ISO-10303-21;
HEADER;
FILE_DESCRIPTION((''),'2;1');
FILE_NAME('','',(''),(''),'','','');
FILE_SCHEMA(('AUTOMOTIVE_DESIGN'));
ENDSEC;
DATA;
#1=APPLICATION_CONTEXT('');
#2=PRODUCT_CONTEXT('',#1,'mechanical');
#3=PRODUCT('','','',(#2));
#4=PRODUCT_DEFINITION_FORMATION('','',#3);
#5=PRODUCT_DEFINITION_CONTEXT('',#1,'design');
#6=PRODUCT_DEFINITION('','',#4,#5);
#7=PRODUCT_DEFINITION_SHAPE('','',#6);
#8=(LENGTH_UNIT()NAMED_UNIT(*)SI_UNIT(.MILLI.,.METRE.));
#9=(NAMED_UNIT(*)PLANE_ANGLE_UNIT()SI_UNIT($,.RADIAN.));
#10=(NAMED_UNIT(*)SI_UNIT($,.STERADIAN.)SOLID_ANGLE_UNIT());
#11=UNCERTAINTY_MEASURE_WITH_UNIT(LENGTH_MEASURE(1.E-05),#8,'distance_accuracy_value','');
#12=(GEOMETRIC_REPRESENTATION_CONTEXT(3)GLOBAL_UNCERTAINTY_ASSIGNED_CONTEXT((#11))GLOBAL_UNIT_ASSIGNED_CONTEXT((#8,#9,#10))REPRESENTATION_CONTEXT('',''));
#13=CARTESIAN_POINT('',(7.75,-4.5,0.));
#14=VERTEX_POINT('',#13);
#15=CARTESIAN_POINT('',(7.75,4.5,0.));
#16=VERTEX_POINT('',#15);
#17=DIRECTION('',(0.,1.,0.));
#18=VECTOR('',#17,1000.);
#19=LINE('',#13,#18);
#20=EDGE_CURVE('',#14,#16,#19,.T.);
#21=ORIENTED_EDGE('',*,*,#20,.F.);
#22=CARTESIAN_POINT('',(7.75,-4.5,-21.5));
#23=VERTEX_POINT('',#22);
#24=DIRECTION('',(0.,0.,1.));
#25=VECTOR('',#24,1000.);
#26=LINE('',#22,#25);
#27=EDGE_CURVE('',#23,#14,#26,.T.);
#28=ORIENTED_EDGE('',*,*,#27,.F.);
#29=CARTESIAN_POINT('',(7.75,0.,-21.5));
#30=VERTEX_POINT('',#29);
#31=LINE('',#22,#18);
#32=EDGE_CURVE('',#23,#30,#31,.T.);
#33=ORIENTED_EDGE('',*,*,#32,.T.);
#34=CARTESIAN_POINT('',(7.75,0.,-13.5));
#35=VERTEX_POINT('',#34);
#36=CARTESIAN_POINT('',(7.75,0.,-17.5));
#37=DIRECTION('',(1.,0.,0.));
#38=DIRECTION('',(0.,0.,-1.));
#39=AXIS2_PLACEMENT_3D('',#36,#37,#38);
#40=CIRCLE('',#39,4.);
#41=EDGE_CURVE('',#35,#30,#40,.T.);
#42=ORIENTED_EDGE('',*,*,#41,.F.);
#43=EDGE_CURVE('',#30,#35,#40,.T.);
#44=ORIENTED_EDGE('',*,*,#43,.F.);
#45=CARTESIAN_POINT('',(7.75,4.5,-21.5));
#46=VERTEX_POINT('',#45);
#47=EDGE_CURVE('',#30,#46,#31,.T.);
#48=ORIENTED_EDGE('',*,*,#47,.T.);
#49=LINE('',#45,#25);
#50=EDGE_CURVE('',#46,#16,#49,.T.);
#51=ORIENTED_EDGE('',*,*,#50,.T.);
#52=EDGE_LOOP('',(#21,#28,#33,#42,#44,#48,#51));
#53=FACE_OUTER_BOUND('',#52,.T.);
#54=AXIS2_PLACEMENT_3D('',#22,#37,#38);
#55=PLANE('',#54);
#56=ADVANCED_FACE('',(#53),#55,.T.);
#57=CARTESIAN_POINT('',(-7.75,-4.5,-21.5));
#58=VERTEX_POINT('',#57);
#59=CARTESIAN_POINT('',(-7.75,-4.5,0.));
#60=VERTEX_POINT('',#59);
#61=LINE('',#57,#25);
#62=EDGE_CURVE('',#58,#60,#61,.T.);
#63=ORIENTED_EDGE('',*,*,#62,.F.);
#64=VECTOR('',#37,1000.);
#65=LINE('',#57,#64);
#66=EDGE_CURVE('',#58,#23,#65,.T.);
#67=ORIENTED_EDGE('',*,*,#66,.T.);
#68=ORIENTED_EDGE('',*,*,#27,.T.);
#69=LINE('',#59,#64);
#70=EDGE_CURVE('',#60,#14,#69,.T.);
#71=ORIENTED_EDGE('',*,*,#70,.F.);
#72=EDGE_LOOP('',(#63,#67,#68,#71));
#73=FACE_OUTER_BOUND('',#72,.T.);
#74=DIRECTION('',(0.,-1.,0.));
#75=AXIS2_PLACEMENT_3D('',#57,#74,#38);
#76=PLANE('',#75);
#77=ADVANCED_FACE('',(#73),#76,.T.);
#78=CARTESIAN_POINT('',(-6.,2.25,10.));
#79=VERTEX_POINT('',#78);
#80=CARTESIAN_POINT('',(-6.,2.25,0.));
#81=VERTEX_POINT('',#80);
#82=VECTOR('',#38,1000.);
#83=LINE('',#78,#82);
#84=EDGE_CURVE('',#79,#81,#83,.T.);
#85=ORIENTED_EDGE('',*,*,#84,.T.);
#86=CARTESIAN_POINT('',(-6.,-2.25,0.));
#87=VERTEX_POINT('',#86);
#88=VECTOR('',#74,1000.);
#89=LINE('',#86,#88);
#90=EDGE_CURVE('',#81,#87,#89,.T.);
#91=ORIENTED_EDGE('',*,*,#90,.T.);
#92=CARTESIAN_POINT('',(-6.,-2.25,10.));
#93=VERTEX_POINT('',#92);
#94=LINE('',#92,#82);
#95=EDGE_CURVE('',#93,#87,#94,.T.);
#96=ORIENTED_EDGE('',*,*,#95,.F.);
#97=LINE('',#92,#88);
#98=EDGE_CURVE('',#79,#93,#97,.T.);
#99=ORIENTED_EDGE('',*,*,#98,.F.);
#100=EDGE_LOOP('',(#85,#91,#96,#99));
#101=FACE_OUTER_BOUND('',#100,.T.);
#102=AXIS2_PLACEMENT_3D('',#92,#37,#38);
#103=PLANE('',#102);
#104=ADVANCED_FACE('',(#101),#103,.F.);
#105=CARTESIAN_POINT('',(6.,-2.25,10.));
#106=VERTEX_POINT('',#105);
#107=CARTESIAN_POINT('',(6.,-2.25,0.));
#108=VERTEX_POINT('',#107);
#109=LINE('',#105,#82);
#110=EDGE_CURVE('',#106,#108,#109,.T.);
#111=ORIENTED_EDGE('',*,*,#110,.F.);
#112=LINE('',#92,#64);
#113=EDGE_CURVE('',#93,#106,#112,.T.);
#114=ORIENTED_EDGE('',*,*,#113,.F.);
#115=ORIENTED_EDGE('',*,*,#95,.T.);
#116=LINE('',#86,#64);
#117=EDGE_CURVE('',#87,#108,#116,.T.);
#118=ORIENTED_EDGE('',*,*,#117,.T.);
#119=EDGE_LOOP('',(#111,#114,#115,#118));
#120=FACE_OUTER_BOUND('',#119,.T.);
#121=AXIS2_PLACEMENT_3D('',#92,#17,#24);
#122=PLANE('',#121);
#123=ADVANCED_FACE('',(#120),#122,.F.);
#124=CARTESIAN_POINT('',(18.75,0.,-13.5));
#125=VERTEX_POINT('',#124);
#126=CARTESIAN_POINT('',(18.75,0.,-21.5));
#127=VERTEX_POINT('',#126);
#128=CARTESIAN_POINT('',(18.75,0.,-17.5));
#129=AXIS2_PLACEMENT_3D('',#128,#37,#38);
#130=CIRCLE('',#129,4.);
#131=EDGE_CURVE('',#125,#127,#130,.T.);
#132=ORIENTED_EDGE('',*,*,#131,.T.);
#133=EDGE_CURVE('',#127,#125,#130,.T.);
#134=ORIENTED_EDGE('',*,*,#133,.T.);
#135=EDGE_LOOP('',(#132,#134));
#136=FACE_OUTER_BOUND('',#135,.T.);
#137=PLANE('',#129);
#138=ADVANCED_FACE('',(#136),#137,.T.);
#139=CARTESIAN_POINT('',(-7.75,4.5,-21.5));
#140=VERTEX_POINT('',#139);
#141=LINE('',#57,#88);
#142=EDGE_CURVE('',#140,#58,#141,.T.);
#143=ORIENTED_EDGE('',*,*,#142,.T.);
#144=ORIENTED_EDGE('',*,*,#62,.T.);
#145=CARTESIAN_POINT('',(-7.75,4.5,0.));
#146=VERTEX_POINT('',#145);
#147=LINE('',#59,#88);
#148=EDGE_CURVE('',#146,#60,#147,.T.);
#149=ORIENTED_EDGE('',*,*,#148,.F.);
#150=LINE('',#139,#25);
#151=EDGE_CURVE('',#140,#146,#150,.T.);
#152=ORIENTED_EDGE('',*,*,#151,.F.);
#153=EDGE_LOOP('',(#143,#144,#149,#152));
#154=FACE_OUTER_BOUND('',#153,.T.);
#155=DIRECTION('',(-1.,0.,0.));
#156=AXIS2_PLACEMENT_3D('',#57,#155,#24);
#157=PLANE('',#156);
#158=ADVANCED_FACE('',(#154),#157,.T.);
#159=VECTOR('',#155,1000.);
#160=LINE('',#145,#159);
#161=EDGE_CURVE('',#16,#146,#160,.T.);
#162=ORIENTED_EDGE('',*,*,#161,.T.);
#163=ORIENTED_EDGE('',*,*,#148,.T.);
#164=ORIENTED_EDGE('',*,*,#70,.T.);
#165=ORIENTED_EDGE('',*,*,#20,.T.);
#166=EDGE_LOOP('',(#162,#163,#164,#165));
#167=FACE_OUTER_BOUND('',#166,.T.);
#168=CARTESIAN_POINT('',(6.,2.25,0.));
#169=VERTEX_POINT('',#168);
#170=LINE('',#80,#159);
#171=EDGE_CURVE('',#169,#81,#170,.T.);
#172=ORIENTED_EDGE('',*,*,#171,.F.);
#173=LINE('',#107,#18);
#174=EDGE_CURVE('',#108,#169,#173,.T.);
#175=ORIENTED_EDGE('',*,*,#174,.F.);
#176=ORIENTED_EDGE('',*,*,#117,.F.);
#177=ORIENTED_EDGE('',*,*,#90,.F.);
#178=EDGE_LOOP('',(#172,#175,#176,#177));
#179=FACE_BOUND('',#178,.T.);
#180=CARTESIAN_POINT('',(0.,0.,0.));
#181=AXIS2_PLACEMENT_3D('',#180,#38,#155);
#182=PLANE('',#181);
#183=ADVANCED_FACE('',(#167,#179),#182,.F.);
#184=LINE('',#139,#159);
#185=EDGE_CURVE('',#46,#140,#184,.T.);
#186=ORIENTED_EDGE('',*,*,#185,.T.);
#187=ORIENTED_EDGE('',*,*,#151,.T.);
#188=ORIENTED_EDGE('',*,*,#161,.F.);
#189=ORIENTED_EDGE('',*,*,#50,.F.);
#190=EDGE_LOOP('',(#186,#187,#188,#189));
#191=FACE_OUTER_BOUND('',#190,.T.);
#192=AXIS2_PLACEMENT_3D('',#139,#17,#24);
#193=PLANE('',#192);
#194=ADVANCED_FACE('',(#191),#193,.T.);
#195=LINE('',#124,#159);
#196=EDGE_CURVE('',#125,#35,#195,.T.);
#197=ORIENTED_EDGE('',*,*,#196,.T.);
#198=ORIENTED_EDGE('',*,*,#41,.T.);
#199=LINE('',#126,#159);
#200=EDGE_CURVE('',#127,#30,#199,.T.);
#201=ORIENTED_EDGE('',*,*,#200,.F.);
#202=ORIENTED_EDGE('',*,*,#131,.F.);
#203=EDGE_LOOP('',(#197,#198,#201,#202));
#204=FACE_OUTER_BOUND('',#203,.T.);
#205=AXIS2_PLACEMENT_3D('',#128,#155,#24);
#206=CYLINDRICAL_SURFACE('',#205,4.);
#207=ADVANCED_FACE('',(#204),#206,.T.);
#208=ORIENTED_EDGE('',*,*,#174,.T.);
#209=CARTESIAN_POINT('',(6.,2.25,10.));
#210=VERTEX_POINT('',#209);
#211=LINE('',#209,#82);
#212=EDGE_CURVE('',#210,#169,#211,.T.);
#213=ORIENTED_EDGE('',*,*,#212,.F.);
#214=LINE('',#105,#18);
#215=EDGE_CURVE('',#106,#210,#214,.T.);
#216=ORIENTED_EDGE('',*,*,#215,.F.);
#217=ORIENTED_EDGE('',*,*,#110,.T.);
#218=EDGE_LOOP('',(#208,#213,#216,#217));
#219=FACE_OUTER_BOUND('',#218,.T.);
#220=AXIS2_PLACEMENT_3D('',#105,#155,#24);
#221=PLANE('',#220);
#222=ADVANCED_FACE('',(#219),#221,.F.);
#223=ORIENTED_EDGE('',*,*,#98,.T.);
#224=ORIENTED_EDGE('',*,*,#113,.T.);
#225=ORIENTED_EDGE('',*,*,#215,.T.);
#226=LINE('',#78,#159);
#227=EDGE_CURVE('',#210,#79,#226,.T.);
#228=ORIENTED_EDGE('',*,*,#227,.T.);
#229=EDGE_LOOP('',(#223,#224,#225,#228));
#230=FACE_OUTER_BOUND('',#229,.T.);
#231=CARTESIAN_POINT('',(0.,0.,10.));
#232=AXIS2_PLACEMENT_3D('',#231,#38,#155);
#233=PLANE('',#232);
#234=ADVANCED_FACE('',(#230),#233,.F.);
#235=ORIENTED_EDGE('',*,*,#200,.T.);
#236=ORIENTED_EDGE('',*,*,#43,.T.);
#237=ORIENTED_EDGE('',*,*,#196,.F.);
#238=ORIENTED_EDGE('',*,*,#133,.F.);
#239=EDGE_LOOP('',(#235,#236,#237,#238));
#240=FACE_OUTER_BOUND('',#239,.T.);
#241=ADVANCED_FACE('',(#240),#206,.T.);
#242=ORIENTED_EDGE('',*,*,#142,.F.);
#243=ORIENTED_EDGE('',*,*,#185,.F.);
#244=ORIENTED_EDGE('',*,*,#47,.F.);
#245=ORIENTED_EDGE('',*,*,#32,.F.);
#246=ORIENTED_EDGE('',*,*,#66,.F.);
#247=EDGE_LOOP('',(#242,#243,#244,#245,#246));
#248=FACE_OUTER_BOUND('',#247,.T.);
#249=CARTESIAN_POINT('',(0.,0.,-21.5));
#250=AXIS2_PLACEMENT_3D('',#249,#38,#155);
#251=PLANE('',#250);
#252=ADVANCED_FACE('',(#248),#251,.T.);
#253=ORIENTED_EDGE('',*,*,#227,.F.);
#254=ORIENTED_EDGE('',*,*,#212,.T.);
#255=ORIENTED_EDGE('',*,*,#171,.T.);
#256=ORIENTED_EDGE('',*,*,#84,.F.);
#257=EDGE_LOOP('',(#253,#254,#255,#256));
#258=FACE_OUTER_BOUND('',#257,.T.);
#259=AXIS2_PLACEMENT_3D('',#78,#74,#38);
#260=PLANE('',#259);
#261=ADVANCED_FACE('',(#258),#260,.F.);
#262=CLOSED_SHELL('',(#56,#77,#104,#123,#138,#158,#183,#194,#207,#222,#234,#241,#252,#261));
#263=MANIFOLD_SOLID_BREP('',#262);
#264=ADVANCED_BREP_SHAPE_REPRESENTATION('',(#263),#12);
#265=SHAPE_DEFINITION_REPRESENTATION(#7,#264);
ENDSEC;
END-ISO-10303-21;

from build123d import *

# Parameters (mm, degrees)
SKETCH_1_W      = 15.5
SKETCH_1_H      = 9
EXTRUDE_1_DEPTH = 21.5
SKETCH_2_R      = 4
EXTRUDE_2_DEPTH = 11
SKETCH_3_W      = 12
SKETCH_3_H      = 4.5
EXTRUDE_3_DEPTH = 10


with BuildPart() as part:
    # 草图1 → 凸台-拉伸1 (new body)
    with BuildSketch(Plane.XY):
        Rectangle(SKETCH_1_W, SKETCH_1_H)
    extrude(amount=-EXTRUDE_1_DEPTH)

    # 草图2 → 凸台-拉伸2 (add)
    with BuildSketch(Plane(origin=(7.75, 0, 0), x_dir=(0, 0, -1), z_dir=(1, 0, 0))):
        with Locations((17.5, 0)):
            Circle(SKETCH_2_R)
    extrude(amount=EXTRUDE_2_DEPTH)

    # 草图3 → 凸台-拉伸3 (add)
    with BuildSketch(Plane.XY):
        Rectangle(SKETCH_3_W, SKETCH_3_H)
    extrude(amount=EXTRUDE_3_DEPTH)


solid = part.part
